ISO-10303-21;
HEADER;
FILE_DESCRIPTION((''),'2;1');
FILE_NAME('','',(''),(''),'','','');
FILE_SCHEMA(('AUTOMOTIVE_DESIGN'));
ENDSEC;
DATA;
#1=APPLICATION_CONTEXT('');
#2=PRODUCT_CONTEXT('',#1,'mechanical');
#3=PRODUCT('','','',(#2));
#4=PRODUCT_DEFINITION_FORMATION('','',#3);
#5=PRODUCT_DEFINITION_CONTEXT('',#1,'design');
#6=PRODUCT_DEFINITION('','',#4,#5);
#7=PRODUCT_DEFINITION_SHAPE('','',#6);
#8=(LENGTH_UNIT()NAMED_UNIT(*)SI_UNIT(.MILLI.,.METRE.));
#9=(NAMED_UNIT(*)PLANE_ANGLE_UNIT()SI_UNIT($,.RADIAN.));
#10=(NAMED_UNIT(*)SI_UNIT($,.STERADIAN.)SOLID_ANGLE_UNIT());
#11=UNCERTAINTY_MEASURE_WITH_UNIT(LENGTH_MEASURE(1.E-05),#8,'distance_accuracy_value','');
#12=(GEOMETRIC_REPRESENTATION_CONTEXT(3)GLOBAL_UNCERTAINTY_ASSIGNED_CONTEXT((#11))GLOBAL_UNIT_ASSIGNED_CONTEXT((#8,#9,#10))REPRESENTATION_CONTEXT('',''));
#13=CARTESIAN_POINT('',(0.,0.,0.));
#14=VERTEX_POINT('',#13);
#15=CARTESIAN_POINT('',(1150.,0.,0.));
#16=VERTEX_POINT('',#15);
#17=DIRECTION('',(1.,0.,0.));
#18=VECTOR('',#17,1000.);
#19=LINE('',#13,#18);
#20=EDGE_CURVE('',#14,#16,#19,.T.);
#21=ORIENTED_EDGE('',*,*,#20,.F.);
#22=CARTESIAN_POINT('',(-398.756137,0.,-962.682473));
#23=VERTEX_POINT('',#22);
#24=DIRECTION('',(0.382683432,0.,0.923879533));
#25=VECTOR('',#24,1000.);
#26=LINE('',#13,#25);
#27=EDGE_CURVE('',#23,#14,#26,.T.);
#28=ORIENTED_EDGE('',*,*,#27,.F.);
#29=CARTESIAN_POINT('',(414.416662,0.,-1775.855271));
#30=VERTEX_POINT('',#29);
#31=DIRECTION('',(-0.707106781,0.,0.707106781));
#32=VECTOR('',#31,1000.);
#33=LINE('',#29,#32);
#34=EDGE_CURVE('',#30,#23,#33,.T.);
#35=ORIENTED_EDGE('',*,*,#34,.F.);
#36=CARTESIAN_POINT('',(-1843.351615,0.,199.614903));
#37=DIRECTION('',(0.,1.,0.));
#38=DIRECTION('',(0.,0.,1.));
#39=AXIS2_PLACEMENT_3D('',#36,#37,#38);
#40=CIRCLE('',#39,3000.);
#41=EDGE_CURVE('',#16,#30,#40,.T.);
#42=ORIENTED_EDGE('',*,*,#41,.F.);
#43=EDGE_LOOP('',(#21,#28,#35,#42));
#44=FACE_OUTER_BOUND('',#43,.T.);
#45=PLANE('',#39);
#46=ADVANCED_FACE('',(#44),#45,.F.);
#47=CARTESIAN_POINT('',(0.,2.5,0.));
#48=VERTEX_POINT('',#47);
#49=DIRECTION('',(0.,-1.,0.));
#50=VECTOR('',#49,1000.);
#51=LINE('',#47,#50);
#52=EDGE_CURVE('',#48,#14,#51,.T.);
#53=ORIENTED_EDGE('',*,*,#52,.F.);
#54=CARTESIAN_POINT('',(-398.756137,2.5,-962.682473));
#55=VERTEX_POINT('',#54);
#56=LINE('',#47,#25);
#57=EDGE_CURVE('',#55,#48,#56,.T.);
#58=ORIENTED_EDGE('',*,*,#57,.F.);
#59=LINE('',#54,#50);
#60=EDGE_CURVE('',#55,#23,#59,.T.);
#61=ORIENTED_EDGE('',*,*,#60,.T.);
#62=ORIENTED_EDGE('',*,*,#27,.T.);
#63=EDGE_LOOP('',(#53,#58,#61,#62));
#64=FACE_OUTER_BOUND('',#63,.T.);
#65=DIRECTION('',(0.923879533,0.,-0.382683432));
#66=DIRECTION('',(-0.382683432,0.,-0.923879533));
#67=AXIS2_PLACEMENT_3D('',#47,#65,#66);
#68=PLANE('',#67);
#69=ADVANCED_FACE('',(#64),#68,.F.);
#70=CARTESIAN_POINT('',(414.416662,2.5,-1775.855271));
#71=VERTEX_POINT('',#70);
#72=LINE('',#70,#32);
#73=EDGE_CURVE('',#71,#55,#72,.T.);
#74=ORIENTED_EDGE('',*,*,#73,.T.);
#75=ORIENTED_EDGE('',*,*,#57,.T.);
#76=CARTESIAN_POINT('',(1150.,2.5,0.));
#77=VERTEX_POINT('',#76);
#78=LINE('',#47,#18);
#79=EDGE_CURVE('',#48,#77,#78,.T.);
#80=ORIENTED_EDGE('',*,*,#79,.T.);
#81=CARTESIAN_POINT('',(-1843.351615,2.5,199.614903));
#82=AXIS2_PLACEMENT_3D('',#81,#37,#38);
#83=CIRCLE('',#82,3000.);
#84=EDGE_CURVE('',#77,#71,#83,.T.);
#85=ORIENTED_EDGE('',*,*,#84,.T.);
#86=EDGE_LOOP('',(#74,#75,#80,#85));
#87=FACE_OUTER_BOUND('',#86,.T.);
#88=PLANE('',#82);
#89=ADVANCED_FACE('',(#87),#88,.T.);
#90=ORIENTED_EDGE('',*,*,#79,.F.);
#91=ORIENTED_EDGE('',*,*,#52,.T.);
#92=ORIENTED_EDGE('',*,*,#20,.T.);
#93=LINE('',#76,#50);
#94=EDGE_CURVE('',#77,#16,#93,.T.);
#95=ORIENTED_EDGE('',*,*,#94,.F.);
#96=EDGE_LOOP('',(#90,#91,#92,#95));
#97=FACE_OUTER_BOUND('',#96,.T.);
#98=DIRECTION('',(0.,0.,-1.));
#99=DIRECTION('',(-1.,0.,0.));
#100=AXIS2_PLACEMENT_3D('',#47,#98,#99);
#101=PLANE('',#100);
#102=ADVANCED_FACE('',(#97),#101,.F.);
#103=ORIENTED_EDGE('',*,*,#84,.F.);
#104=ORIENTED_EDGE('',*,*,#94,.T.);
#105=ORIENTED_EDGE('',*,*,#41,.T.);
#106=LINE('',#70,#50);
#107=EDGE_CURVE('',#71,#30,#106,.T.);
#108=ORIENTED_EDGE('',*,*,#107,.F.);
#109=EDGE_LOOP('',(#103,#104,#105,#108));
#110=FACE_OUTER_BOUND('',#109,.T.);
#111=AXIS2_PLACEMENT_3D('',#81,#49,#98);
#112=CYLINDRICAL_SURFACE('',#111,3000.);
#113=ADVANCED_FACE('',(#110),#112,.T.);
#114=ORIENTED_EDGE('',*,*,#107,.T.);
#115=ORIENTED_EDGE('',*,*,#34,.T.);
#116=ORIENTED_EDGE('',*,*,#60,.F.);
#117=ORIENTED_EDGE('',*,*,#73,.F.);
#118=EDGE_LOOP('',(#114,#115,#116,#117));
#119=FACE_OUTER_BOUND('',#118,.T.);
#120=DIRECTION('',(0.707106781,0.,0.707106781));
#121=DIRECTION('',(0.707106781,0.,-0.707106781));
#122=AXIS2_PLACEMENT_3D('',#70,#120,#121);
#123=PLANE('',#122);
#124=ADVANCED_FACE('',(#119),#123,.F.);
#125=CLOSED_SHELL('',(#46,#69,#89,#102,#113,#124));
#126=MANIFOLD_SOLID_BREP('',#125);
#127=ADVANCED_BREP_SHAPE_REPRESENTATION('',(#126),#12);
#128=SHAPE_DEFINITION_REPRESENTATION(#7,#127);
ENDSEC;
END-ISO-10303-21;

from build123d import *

# Parameters (mm, degrees)
BOSS_EXTRUDE2_DEPTH = 2.5


with BuildPart() as part:
    # Sketch2 → Boss-Extrude2 (new body)
    with BuildSketch(Plane(origin=(0, 0, 0), x_dir=(1, 0, 0), z_dir=(0, 1, 0))):
        with BuildLine():
            Line((0, 0), (-398.756136524, 962.682472877))
            Line((-398.756136524, 962.682472877), (414.41666184, 1775.855271241))
            ThreePointArc((414.41666184, 1775.855271241), (928.286982606, 948.435394322), (1150, 0))
            Line((1150, 0), (0, 0))
        make_face()
    extrude(amount=BOSS_EXTRUDE2_DEPTH)


solid = part.part
